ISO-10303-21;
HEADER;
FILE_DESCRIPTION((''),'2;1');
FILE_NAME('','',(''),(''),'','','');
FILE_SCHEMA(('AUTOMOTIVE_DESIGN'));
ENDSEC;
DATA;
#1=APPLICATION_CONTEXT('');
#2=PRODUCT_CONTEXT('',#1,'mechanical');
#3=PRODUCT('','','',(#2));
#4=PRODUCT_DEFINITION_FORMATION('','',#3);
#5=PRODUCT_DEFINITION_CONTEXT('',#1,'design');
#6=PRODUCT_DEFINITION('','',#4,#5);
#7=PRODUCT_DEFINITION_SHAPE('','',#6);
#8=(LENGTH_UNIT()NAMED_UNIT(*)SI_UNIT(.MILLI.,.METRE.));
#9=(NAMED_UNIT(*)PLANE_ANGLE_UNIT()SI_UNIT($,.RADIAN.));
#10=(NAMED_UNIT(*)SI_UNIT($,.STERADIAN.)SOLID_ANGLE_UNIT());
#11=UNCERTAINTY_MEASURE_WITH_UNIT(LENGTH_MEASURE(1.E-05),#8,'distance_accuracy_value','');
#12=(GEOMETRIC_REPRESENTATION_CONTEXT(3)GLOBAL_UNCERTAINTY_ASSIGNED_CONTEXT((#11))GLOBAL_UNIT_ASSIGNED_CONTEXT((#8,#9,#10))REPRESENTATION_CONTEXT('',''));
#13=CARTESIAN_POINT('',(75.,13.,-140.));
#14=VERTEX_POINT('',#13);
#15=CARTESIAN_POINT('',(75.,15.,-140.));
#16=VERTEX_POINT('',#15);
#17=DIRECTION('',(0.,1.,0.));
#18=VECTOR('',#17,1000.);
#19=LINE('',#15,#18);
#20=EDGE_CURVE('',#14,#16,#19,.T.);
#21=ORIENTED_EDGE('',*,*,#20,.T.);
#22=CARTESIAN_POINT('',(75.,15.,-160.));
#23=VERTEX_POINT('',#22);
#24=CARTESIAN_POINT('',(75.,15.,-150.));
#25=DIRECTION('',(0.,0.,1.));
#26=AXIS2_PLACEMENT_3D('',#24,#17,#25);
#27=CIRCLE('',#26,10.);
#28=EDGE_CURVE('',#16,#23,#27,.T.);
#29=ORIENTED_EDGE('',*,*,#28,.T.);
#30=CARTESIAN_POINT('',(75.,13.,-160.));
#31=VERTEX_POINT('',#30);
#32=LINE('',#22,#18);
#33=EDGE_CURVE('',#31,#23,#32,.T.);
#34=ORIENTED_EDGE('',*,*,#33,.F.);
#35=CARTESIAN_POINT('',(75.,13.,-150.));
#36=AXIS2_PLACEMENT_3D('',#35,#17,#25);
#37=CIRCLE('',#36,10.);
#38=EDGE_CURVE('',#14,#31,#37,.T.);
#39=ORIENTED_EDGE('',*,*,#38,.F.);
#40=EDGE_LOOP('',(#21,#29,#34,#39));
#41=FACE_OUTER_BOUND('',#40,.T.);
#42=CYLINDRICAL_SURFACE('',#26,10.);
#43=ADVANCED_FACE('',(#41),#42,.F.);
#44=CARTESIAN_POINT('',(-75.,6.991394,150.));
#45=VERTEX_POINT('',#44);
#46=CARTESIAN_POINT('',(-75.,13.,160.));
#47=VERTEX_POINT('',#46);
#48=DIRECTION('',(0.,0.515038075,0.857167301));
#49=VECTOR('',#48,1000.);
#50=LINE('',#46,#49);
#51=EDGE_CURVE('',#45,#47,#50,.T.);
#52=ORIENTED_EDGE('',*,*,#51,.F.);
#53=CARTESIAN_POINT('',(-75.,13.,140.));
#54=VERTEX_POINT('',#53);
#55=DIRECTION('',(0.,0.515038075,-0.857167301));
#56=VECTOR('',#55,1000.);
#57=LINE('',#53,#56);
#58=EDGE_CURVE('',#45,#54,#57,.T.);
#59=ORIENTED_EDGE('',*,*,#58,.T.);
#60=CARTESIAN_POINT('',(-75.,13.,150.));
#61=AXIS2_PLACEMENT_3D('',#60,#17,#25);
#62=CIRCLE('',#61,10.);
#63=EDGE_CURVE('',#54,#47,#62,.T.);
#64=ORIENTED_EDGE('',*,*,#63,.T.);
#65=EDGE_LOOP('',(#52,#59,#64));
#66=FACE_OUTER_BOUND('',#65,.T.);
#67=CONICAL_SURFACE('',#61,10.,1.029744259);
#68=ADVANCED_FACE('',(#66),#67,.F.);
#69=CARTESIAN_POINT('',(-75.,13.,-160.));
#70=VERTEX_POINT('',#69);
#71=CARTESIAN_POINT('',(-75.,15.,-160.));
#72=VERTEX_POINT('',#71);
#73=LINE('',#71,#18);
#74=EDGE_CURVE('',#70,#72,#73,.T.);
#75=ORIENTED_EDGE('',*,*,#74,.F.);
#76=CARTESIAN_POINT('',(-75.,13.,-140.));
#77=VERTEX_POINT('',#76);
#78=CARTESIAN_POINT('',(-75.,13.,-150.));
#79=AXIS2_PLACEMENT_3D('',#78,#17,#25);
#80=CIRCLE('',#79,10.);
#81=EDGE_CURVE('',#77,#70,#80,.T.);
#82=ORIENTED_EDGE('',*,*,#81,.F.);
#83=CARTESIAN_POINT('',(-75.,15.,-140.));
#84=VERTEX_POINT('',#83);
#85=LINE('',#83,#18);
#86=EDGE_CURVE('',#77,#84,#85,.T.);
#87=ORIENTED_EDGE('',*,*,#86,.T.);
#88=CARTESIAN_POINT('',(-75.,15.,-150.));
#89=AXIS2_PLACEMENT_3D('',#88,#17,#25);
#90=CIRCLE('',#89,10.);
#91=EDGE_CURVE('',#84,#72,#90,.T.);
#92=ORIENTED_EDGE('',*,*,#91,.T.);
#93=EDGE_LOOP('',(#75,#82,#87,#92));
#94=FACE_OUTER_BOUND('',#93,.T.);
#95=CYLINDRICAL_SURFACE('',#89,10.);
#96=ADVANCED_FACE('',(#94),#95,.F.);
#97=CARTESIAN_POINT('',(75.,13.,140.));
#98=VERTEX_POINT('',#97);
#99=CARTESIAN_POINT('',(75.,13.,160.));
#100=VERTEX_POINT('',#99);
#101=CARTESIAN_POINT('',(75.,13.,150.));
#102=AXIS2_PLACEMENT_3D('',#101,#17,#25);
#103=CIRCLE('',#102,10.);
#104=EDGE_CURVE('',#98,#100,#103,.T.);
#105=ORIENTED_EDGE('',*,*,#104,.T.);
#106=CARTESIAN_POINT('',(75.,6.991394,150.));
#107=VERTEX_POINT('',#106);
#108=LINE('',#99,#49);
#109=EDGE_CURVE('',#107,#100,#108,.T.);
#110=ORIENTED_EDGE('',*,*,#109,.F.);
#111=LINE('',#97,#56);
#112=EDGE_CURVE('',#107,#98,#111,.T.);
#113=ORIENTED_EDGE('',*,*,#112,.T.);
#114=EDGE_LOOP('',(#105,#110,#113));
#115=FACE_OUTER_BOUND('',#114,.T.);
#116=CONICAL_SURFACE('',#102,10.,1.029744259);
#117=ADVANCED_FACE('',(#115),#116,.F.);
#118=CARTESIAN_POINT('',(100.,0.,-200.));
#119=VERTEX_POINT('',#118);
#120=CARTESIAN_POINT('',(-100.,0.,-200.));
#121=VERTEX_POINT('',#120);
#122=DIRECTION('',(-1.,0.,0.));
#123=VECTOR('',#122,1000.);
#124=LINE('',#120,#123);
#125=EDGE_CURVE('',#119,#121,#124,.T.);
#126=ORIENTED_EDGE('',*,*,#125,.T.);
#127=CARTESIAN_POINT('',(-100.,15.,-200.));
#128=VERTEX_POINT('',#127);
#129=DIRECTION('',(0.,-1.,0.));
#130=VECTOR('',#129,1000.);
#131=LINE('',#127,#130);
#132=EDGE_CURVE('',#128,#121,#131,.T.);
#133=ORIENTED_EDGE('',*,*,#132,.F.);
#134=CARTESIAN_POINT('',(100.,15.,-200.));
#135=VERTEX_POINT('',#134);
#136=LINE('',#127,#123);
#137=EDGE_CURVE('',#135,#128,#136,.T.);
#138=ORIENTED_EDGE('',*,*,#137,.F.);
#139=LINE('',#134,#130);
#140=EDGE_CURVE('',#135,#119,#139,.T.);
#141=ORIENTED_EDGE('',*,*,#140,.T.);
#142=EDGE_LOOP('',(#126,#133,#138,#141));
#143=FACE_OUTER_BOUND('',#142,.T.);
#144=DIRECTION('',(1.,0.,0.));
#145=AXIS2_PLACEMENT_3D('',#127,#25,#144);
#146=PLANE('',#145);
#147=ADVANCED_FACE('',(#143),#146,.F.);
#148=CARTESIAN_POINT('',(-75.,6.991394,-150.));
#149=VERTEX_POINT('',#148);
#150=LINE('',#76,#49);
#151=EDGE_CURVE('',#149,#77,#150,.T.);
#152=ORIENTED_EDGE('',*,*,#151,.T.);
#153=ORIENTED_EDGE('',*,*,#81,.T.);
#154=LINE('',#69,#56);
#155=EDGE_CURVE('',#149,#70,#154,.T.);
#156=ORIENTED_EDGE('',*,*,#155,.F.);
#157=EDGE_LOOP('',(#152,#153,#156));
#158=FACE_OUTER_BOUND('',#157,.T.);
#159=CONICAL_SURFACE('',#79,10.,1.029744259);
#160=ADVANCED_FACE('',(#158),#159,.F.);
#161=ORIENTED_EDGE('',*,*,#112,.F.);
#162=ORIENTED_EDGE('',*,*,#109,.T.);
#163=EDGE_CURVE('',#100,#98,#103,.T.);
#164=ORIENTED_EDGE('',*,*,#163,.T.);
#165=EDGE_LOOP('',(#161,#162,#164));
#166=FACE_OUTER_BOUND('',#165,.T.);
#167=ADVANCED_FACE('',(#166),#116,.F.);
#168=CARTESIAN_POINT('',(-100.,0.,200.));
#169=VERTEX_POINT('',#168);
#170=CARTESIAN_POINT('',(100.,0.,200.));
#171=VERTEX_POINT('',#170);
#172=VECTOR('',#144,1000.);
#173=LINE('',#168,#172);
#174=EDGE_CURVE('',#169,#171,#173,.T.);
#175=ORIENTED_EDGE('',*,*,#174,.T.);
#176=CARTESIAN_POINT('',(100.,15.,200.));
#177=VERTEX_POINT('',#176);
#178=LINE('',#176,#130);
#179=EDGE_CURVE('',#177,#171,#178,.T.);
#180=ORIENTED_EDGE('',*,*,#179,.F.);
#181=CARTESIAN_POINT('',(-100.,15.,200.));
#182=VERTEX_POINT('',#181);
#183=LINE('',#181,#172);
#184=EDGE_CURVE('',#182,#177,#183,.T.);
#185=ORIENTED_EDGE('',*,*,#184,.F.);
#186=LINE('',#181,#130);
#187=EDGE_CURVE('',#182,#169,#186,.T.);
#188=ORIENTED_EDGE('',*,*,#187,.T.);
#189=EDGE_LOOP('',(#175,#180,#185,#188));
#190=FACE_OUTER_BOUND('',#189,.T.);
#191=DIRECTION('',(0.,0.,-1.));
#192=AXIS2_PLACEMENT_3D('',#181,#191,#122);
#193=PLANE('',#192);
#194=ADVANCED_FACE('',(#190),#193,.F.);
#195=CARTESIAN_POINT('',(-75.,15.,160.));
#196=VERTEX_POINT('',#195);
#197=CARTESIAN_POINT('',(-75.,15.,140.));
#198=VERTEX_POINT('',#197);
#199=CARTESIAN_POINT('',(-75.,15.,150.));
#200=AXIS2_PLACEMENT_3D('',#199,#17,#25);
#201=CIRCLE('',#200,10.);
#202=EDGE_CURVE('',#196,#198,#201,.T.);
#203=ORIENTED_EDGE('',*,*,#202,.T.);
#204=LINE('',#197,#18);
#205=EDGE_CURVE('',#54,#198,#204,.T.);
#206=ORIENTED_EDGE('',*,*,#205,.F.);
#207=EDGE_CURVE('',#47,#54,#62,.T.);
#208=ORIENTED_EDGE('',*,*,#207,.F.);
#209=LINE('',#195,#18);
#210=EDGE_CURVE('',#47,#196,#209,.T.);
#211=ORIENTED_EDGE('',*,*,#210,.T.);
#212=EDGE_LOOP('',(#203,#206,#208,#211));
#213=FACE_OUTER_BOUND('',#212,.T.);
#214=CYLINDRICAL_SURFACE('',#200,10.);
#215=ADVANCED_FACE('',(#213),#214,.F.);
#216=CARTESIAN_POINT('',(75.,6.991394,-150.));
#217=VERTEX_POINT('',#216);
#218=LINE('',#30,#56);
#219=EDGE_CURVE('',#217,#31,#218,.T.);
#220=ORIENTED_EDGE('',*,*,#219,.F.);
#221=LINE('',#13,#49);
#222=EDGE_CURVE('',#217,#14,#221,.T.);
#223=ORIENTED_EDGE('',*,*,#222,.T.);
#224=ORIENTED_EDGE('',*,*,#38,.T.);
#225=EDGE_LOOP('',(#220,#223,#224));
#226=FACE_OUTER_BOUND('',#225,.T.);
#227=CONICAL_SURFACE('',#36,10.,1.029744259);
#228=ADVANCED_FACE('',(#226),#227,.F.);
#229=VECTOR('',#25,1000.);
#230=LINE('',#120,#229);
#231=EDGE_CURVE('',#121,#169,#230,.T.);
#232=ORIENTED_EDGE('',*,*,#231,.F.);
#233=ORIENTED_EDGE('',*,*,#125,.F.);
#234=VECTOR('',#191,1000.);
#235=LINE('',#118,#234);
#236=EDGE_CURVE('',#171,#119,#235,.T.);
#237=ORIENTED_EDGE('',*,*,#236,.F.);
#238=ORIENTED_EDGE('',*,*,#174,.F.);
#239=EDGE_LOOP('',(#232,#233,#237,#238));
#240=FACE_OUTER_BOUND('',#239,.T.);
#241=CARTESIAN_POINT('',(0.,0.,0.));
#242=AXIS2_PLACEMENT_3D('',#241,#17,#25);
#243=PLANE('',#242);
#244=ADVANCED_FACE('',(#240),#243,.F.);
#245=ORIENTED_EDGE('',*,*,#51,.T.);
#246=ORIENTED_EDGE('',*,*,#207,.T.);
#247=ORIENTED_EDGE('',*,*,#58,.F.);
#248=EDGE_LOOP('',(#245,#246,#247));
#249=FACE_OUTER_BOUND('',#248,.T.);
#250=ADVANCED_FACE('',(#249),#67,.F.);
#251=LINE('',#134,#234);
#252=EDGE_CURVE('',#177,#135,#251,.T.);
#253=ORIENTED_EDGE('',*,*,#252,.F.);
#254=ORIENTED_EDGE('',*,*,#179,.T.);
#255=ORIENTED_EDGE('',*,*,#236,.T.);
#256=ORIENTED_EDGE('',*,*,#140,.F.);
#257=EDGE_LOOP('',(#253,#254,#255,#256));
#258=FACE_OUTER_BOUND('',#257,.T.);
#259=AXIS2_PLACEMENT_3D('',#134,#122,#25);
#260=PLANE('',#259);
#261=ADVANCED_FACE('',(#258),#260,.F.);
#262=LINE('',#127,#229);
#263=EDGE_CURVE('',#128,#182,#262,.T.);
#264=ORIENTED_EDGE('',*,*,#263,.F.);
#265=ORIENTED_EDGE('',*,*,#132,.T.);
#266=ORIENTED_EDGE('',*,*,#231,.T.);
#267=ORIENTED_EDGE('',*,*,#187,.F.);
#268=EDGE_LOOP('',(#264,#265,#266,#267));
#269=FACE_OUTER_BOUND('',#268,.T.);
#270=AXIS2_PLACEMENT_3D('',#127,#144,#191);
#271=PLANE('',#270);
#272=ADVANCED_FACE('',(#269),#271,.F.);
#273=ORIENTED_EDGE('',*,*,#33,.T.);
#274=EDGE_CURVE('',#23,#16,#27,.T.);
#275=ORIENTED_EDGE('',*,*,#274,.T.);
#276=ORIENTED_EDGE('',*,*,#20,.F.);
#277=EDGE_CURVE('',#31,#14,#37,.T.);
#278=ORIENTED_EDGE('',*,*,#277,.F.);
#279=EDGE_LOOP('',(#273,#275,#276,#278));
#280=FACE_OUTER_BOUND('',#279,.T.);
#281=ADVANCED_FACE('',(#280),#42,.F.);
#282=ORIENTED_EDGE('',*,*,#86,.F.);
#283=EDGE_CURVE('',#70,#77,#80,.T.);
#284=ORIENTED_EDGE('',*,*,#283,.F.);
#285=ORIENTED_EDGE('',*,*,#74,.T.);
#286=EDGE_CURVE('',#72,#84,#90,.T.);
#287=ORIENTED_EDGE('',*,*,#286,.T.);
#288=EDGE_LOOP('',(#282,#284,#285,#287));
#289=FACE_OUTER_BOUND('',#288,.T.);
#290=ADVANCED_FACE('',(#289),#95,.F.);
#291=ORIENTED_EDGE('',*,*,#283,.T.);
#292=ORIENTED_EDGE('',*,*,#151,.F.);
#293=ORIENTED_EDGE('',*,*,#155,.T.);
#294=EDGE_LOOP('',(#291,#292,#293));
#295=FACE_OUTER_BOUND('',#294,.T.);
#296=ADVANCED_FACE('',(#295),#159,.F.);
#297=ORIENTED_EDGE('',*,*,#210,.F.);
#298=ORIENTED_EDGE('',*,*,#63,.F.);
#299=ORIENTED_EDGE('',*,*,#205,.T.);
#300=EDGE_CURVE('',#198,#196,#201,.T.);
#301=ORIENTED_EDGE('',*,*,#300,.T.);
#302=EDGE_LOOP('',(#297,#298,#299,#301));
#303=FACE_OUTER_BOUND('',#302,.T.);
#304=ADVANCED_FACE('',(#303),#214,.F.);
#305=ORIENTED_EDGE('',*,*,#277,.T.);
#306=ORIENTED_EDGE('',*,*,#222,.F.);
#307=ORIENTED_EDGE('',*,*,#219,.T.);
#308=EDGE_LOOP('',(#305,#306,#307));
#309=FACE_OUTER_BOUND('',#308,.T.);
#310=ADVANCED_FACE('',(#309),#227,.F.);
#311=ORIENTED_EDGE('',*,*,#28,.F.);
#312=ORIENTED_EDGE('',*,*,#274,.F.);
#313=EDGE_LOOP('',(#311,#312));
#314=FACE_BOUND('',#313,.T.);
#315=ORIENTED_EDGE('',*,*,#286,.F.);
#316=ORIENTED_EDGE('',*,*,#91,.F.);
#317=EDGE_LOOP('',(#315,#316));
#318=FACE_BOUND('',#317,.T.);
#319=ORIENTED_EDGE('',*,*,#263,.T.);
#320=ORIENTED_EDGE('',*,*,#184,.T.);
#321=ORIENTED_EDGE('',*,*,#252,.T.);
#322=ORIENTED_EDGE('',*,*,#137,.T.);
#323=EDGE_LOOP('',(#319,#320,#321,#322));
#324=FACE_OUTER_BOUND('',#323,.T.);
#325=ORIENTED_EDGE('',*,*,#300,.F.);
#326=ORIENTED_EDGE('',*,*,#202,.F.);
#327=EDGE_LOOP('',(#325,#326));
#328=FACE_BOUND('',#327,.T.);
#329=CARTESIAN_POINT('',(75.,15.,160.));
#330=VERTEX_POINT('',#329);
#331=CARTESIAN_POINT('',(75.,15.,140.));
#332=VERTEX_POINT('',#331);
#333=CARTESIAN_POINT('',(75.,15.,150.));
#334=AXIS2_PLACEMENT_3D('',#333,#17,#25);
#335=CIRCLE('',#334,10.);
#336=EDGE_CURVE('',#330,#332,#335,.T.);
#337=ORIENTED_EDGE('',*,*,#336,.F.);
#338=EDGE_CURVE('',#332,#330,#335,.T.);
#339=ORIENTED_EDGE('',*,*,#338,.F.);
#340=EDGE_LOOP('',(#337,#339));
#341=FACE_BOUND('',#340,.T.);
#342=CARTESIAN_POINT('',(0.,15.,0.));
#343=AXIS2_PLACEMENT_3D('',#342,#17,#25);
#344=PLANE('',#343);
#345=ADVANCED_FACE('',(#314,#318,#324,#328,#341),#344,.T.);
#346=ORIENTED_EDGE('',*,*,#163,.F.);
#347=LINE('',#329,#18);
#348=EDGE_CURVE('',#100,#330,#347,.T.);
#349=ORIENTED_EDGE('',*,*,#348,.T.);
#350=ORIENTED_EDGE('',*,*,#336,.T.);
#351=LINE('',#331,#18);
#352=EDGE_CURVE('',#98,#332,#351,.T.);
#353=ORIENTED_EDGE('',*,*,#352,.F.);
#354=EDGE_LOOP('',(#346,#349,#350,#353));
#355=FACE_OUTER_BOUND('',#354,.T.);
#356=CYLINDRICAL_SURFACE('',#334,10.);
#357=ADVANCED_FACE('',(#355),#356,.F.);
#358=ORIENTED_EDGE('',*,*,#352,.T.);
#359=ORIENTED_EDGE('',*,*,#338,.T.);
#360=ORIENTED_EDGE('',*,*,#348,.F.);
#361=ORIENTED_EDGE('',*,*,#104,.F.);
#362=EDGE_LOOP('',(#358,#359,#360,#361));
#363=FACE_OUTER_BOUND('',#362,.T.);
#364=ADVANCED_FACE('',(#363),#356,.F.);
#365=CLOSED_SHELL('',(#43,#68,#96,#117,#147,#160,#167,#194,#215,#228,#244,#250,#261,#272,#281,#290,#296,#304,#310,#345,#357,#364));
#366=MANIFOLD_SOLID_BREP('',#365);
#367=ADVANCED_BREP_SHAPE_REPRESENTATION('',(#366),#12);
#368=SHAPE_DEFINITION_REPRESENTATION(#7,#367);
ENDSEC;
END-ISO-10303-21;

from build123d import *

# Parameters (mm, degrees)
SKETCH1_W                      = 200
SKETCH1_H                      = 400
BOSS_EXTRUDE1_DEPTH            = 15
F_20_0_20_DIAMETER_HOLE1_D     = 20
F_20_0_20_DIAMETER_HOLE1_DEPTH = 2
F_20_0_20_DIAMETER_HOLE1_TIP   = 6.00860619


with BuildPart() as part:
    # Sketch1 → Boss-Extrude1 (new body)
    with BuildSketch(Plane(origin=(0, 0, 0), x_dir=(1, 0, 0), z_dir=(0, 1, 0))):
        Rectangle(SKETCH1_W, SKETCH1_H)
    extrude(amount=BOSS_EXTRUDE1_DEPTH)

    # Ø20.0 (20) Diameter Hole1
    with Locations(Plane(origin=(0, 15, 0), x_dir=(1, 0, 0), z_dir=(0, 1, 0))):
        with Locations((-75, 150), (-75, -150), (75, -150), (75, 150)):
            Hole(F_20_0_20_DIAMETER_HOLE1_D / 2, depth=F_20_0_20_DIAMETER_HOLE1_DEPTH)
            with Locations((0, 0, -(F_20_0_20_DIAMETER_HOLE1_DEPTH + F_20_0_20_DIAMETER_HOLE1_TIP / 2))):  # 118° drill point
                Cone(0, F_20_0_20_DIAMETER_HOLE1_D / 2, F_20_0_20_DIAMETER_HOLE1_TIP, mode=Mode.SUBTRACT)


solid = part.part
